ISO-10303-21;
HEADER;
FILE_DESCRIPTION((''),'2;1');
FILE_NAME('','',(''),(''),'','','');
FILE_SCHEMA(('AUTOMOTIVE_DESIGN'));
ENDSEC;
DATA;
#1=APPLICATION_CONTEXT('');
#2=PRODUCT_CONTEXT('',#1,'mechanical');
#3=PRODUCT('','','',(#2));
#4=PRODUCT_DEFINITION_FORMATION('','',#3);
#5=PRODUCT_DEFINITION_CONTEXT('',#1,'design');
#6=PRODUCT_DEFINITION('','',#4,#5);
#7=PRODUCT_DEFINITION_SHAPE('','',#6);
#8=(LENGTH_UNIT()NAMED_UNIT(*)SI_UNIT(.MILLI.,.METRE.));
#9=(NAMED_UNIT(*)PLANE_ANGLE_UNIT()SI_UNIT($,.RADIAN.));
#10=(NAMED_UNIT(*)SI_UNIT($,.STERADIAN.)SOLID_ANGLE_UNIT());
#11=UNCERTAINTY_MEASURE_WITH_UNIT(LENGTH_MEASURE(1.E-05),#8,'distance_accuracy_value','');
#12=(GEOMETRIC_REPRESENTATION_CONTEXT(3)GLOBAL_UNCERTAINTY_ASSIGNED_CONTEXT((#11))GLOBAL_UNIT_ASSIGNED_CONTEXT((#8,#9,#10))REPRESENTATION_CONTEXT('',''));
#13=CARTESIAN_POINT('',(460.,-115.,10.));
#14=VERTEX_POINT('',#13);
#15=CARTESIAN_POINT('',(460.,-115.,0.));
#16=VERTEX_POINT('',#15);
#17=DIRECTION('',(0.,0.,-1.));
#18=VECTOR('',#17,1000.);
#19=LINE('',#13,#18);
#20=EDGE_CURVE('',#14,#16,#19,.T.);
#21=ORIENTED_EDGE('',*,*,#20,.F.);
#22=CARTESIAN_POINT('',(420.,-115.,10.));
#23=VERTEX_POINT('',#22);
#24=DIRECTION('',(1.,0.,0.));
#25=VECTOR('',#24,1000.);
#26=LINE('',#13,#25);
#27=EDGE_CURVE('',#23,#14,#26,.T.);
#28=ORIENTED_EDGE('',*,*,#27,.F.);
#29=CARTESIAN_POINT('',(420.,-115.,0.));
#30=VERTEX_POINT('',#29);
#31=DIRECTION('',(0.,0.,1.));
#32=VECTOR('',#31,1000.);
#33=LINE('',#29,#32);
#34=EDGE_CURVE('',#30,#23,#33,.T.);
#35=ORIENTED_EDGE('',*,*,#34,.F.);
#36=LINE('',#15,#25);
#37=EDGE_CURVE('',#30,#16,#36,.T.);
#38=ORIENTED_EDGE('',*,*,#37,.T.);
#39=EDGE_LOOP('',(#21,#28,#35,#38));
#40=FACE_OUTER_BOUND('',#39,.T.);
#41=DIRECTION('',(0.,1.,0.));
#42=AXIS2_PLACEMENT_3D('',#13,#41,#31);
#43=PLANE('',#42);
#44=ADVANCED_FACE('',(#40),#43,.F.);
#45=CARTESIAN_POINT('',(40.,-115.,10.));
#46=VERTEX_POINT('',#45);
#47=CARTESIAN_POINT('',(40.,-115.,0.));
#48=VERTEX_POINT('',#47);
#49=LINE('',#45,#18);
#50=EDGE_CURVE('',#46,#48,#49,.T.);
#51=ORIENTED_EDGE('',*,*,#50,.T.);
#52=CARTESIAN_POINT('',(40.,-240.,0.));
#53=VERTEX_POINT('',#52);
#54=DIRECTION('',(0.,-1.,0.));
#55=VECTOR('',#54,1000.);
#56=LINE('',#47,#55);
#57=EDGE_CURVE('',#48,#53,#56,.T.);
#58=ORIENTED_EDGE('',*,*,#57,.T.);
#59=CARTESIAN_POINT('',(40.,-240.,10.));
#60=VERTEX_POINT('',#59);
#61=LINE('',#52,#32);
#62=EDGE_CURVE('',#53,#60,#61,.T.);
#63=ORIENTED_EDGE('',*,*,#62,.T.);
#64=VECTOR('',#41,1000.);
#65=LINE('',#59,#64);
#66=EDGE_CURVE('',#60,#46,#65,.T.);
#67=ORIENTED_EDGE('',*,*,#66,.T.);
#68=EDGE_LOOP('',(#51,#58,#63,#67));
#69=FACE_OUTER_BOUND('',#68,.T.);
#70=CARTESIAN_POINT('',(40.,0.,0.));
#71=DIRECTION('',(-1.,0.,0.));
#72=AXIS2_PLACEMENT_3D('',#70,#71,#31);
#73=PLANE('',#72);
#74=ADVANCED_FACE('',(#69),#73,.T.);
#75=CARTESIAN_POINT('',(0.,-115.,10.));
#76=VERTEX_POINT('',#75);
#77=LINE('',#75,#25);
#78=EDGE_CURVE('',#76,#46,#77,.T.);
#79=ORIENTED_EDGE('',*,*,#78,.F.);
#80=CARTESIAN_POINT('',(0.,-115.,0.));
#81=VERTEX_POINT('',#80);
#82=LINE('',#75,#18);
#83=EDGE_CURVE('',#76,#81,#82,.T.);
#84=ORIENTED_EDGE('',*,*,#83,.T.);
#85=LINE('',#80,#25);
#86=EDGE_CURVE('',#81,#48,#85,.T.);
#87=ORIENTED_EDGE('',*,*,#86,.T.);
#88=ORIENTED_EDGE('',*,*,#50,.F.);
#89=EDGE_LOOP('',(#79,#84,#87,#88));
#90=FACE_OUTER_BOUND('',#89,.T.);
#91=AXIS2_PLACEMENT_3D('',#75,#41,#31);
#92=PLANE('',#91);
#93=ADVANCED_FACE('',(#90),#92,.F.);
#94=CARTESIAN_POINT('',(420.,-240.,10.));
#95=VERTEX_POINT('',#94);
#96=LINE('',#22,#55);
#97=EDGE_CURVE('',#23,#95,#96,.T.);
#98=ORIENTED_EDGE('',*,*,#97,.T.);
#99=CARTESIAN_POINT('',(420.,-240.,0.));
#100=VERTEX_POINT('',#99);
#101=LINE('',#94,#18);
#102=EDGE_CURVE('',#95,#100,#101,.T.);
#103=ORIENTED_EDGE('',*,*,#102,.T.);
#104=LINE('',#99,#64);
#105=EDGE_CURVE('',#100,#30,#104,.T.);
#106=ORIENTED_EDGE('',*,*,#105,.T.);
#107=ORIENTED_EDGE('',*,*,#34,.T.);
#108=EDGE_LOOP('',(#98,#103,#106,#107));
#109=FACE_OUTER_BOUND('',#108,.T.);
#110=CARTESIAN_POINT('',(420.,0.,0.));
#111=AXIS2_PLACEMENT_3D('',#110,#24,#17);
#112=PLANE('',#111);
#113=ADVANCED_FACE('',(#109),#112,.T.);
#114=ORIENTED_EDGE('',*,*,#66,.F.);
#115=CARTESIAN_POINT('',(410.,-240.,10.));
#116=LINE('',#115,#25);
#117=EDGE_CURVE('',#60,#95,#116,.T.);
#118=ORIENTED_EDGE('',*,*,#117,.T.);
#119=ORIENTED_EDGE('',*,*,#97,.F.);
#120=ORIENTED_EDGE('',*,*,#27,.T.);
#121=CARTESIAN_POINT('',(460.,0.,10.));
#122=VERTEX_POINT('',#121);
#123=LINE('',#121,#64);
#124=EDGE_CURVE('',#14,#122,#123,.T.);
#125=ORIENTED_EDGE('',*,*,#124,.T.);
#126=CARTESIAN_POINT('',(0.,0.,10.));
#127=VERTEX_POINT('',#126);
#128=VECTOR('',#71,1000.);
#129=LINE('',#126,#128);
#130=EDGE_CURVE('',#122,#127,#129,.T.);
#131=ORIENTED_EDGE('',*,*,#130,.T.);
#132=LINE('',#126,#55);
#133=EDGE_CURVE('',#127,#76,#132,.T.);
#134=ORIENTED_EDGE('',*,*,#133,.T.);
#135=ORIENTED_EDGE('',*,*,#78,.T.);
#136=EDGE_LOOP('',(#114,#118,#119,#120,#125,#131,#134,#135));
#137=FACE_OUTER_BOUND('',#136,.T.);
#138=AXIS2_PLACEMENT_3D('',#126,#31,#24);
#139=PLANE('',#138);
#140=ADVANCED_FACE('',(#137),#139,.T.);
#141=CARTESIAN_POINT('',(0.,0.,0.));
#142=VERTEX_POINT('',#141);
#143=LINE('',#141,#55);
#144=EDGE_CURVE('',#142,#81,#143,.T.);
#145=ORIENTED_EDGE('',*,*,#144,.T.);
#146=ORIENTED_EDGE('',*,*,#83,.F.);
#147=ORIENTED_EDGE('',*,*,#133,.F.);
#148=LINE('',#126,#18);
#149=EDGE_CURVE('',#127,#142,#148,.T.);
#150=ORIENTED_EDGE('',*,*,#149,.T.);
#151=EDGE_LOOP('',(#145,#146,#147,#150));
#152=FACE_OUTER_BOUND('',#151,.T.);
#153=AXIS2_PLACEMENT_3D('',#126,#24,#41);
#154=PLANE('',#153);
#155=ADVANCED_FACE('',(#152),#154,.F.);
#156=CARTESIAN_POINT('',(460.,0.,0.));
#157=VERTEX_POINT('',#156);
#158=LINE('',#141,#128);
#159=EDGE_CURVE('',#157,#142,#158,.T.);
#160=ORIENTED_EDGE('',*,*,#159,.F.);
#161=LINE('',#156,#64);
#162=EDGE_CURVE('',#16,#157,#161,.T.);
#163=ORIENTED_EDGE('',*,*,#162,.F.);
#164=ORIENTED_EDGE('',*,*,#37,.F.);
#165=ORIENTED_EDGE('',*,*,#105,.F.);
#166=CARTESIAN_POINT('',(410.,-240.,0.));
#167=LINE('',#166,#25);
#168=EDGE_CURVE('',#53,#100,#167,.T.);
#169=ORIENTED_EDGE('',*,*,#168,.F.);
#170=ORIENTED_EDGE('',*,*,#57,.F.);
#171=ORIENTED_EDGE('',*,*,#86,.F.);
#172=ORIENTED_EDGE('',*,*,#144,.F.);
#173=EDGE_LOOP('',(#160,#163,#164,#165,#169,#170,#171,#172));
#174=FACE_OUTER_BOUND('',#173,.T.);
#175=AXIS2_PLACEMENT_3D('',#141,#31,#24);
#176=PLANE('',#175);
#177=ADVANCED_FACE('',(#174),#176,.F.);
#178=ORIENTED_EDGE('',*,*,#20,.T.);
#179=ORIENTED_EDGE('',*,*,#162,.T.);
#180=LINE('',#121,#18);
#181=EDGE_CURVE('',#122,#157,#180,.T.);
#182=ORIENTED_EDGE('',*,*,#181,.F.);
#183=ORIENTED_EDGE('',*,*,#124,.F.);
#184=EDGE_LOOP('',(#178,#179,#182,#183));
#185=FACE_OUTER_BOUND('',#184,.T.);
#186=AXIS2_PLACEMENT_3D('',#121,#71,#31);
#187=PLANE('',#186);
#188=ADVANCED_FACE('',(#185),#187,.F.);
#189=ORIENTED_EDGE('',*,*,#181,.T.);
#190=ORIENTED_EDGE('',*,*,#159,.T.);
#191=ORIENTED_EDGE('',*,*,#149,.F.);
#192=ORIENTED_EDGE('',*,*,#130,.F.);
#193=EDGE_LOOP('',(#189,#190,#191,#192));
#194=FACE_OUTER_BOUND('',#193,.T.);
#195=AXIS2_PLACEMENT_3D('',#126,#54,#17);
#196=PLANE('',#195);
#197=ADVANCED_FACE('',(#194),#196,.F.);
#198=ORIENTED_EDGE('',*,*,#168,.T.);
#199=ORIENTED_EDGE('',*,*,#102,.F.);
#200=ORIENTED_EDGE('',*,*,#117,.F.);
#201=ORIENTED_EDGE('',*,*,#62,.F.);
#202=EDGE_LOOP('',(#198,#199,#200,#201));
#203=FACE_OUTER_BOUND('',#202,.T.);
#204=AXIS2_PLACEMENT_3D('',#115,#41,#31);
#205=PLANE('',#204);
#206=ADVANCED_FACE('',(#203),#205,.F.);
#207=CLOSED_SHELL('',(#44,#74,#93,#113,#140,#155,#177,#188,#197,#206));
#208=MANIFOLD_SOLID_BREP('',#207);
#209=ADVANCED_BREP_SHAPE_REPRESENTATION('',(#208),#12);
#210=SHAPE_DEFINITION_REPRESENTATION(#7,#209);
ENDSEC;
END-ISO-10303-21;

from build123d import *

# Parameters (mm, degrees)
EXTRUDE_1_DEPTH = 10
SKETCH_2_W      = 10
SKETCH_2_H      = 125
EXTRUDE_2_DEPTH = 10
SKETCH_3_W      = 10
SKETCH_3_H      = 125
EXTRUDE_3_DEPTH = 10


with BuildPart() as part:
    # 草图1 → 凸台-拉伸1 (new body)
    with BuildSketch(Plane.XY):
        Polygon((0, 0), (460, 0), (460, -115), (410, -115), (410, -240), (50, -240), (50, -115), (0, -115), align=None)
    extrude(amount=EXTRUDE_1_DEPTH)

    # 草图2 → 凸台-拉伸2 (add)
    with BuildSketch(Plane(origin=(410, 0, 0), x_dir=(0, 0, -1), z_dir=(1, 0, 0))):
        with Locations((-5, -177.5)):
            Rectangle(SKETCH_2_W, SKETCH_2_H)
    extrude(amount=EXTRUDE_2_DEPTH)

    # 草图3 → 凸台-拉伸3 (add)
    with BuildSketch(Plane.ZY.offset(-50)):
        with Locations((5, -177.5)):
            Rectangle(SKETCH_3_W, SKETCH_3_H)
    extrude(amount=EXTRUDE_3_DEPTH)


solid = part.part
